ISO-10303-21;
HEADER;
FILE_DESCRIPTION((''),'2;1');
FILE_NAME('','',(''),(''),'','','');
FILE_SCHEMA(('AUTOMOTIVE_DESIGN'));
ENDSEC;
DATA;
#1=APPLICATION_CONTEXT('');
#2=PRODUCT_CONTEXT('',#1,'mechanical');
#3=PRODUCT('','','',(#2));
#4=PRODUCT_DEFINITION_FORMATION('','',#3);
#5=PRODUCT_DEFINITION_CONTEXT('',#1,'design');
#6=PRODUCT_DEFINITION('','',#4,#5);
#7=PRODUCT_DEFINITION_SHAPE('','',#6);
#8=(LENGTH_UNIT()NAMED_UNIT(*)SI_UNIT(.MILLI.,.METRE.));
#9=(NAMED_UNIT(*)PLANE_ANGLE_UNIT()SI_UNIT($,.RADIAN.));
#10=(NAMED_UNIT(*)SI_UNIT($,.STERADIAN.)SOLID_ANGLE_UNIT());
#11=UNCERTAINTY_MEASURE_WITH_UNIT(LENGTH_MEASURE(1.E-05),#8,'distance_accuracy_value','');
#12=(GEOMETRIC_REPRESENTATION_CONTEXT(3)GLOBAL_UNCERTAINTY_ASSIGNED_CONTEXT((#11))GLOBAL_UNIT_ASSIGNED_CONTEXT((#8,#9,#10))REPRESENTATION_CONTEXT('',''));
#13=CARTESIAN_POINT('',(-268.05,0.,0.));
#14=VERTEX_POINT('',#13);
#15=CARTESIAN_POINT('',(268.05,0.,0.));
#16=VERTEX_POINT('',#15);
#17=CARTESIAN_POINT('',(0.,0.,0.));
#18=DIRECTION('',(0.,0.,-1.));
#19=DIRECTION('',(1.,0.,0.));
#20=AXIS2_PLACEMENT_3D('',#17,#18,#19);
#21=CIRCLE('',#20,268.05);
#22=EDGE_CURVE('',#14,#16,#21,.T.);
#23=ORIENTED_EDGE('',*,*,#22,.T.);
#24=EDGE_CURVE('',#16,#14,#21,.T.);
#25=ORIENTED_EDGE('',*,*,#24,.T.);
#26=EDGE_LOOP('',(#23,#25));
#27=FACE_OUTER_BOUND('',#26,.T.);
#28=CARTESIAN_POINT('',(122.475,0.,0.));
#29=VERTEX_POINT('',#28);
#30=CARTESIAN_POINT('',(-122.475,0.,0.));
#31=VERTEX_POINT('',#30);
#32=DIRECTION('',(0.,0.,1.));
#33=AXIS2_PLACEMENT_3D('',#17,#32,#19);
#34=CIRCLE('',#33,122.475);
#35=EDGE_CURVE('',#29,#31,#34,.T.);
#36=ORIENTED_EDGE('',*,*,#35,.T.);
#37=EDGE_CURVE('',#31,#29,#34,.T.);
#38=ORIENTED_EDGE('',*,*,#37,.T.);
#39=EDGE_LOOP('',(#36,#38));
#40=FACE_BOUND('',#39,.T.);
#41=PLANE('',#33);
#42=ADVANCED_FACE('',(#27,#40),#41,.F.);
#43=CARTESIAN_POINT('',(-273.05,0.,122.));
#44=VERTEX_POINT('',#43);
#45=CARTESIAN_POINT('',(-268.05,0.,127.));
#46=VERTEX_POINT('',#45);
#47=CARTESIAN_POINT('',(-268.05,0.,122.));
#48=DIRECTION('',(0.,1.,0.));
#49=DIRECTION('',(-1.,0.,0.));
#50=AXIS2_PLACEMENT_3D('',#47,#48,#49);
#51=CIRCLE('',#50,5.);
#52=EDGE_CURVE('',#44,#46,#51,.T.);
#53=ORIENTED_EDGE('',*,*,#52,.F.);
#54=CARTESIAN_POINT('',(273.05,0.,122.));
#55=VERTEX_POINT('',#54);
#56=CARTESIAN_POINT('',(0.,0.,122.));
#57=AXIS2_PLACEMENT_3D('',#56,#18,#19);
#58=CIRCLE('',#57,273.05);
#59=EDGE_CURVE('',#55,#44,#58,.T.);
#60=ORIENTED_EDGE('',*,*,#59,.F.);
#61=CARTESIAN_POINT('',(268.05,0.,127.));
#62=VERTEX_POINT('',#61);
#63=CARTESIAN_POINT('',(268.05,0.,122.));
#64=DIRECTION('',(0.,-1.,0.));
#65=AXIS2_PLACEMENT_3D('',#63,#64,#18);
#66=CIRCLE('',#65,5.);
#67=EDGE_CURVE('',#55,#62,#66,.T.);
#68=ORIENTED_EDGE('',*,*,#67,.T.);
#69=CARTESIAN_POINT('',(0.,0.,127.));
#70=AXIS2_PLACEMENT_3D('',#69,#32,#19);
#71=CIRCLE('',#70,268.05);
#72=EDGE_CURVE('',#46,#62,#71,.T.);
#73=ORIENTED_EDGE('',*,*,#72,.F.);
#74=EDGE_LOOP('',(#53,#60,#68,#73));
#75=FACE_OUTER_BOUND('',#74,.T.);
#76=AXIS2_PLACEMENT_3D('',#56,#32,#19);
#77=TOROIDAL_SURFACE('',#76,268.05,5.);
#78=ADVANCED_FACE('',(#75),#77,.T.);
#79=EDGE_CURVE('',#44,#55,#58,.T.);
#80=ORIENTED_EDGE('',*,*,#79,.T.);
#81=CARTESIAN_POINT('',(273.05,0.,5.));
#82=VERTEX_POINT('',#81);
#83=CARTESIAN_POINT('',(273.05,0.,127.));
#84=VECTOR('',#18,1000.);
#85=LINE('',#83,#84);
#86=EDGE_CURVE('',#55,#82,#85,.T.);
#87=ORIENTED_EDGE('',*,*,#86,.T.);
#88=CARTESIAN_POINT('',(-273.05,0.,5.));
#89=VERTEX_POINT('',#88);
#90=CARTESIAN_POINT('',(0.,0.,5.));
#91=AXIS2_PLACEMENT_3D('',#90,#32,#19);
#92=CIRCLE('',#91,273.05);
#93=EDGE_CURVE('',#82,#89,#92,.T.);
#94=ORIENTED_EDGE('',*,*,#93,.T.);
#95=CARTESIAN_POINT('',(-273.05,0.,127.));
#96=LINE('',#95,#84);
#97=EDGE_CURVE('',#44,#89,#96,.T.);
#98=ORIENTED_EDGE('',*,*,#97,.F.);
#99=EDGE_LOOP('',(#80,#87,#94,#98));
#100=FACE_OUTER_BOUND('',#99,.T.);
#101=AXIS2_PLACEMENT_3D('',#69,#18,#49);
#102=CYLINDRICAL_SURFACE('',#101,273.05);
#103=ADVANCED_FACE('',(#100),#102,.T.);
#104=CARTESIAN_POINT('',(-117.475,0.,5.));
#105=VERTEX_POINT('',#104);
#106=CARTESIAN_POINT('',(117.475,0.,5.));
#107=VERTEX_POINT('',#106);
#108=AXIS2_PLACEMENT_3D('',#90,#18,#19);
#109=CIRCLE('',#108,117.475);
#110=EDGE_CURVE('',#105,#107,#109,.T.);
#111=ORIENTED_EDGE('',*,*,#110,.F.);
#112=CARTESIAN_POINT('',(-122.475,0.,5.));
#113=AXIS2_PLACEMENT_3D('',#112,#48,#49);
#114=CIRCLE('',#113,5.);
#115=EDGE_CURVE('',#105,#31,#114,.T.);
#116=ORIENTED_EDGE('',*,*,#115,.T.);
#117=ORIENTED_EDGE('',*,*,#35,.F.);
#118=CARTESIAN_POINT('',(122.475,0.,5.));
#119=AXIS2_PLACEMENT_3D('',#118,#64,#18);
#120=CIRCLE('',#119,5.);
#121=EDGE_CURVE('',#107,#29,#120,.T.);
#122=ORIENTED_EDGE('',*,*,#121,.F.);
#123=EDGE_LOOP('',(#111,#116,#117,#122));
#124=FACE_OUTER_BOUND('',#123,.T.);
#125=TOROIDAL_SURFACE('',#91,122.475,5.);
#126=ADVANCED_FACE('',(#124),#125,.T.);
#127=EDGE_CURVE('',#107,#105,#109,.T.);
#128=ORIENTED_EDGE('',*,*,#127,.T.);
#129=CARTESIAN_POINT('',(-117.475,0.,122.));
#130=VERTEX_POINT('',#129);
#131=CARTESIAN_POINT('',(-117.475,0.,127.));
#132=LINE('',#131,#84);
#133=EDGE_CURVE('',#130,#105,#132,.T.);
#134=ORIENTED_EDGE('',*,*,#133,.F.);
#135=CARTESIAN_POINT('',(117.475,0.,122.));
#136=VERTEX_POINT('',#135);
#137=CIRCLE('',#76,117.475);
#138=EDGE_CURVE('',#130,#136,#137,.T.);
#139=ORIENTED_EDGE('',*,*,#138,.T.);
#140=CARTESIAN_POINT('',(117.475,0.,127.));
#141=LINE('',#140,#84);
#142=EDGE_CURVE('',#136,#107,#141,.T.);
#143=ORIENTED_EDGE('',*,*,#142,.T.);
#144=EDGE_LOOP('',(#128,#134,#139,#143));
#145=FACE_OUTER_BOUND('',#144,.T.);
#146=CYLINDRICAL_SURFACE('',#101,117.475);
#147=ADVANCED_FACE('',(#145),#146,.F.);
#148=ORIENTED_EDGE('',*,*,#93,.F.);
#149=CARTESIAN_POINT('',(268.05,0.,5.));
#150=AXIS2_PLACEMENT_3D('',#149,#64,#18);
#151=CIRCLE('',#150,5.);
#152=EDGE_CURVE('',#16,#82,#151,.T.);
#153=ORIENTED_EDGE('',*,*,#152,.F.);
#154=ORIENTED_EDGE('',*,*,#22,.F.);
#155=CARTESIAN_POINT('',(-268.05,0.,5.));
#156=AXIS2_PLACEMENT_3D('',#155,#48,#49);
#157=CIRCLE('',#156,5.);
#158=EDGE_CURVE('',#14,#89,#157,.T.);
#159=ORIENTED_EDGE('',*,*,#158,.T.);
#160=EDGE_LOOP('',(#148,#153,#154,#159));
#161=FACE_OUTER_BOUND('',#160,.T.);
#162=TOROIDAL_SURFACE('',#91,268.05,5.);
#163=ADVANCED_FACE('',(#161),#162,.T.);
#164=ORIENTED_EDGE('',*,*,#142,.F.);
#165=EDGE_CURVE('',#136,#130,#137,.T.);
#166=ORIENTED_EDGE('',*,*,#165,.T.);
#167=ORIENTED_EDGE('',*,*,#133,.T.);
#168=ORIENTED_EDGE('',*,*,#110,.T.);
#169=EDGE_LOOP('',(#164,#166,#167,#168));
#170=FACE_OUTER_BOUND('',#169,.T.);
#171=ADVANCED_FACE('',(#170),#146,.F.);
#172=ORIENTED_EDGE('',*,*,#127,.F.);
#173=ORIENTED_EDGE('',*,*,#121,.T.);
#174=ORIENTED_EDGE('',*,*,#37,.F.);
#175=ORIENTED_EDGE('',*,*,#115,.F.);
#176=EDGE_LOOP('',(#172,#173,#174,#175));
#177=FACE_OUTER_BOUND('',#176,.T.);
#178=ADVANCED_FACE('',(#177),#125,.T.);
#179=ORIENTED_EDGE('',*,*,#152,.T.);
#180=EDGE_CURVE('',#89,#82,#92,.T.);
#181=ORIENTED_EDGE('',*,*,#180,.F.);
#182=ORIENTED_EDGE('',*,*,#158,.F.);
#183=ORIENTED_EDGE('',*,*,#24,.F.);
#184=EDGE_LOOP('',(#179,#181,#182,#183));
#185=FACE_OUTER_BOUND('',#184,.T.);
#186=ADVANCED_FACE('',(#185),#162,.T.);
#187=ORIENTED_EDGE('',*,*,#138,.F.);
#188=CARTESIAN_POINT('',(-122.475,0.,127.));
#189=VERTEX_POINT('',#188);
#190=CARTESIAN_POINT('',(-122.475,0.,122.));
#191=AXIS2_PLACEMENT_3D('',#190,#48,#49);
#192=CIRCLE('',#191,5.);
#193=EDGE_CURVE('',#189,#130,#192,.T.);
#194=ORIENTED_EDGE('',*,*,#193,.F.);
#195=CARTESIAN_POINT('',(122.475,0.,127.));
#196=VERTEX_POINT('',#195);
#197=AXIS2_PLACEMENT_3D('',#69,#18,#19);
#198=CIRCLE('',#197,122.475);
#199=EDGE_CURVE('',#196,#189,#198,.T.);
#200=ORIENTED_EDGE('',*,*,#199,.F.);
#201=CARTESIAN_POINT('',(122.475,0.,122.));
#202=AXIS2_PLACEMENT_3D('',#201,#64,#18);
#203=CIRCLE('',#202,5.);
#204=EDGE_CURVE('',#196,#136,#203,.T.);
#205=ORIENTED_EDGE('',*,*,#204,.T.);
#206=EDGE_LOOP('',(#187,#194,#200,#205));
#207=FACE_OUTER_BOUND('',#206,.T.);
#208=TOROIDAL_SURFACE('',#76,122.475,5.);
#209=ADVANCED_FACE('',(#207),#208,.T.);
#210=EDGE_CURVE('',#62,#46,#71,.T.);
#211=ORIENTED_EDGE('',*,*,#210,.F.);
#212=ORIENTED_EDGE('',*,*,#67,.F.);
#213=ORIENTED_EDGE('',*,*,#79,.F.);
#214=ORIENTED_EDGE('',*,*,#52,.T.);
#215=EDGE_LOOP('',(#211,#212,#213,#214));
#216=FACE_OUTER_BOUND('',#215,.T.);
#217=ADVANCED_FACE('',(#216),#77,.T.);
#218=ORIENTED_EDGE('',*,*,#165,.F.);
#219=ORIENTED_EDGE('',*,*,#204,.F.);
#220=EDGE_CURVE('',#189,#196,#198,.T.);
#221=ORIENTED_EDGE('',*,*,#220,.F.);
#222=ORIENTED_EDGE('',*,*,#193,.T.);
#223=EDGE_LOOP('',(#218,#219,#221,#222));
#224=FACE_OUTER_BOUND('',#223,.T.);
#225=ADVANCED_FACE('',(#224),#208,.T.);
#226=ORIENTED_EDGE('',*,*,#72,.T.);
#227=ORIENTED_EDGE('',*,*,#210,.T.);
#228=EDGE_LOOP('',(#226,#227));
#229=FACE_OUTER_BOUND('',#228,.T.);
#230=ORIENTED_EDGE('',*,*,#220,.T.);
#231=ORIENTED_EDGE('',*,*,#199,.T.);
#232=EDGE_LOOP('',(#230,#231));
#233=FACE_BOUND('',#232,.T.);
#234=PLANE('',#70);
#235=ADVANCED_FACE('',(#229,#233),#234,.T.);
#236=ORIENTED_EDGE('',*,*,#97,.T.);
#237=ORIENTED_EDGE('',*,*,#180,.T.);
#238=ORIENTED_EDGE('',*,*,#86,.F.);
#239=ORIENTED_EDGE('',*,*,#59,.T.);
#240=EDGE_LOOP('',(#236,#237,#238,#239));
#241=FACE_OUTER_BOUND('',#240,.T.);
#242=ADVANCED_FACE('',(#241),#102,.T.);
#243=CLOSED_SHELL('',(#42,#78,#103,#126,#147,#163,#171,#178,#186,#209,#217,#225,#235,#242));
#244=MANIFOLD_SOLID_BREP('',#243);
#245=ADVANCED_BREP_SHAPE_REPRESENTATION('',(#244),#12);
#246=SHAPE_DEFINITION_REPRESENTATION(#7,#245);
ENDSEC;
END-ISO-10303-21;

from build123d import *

# Parameters (mm, degrees)
SKETCH1_R           = 273.05
SKETCH1_R_2         = 117.475
BOSS_EXTRUDE1_DEPTH = 127
FILLET1_R           = 5


with BuildPart() as part:
    # Sketch1 → Boss-Extrude1 (new body)
    with BuildSketch(Plane.XY):
        Circle(SKETCH1_R)
        Circle(SKETCH1_R_2, mode=Mode.SUBTRACT)
    extrude(amount=BOSS_EXTRUDE1_DEPTH)

    # Fillet1
    fillet1_edges = [part.edges().sort_by_distance(p)[0] for p in [
        (-273.05, 0, 0),
        (-273.05, 0, 127),
        (-117.475, 0, 0),
        (-117.475, 0, 127),
    ]]
    fillet(fillet1_edges, radius=FILLET1_R)


solid = part.part
